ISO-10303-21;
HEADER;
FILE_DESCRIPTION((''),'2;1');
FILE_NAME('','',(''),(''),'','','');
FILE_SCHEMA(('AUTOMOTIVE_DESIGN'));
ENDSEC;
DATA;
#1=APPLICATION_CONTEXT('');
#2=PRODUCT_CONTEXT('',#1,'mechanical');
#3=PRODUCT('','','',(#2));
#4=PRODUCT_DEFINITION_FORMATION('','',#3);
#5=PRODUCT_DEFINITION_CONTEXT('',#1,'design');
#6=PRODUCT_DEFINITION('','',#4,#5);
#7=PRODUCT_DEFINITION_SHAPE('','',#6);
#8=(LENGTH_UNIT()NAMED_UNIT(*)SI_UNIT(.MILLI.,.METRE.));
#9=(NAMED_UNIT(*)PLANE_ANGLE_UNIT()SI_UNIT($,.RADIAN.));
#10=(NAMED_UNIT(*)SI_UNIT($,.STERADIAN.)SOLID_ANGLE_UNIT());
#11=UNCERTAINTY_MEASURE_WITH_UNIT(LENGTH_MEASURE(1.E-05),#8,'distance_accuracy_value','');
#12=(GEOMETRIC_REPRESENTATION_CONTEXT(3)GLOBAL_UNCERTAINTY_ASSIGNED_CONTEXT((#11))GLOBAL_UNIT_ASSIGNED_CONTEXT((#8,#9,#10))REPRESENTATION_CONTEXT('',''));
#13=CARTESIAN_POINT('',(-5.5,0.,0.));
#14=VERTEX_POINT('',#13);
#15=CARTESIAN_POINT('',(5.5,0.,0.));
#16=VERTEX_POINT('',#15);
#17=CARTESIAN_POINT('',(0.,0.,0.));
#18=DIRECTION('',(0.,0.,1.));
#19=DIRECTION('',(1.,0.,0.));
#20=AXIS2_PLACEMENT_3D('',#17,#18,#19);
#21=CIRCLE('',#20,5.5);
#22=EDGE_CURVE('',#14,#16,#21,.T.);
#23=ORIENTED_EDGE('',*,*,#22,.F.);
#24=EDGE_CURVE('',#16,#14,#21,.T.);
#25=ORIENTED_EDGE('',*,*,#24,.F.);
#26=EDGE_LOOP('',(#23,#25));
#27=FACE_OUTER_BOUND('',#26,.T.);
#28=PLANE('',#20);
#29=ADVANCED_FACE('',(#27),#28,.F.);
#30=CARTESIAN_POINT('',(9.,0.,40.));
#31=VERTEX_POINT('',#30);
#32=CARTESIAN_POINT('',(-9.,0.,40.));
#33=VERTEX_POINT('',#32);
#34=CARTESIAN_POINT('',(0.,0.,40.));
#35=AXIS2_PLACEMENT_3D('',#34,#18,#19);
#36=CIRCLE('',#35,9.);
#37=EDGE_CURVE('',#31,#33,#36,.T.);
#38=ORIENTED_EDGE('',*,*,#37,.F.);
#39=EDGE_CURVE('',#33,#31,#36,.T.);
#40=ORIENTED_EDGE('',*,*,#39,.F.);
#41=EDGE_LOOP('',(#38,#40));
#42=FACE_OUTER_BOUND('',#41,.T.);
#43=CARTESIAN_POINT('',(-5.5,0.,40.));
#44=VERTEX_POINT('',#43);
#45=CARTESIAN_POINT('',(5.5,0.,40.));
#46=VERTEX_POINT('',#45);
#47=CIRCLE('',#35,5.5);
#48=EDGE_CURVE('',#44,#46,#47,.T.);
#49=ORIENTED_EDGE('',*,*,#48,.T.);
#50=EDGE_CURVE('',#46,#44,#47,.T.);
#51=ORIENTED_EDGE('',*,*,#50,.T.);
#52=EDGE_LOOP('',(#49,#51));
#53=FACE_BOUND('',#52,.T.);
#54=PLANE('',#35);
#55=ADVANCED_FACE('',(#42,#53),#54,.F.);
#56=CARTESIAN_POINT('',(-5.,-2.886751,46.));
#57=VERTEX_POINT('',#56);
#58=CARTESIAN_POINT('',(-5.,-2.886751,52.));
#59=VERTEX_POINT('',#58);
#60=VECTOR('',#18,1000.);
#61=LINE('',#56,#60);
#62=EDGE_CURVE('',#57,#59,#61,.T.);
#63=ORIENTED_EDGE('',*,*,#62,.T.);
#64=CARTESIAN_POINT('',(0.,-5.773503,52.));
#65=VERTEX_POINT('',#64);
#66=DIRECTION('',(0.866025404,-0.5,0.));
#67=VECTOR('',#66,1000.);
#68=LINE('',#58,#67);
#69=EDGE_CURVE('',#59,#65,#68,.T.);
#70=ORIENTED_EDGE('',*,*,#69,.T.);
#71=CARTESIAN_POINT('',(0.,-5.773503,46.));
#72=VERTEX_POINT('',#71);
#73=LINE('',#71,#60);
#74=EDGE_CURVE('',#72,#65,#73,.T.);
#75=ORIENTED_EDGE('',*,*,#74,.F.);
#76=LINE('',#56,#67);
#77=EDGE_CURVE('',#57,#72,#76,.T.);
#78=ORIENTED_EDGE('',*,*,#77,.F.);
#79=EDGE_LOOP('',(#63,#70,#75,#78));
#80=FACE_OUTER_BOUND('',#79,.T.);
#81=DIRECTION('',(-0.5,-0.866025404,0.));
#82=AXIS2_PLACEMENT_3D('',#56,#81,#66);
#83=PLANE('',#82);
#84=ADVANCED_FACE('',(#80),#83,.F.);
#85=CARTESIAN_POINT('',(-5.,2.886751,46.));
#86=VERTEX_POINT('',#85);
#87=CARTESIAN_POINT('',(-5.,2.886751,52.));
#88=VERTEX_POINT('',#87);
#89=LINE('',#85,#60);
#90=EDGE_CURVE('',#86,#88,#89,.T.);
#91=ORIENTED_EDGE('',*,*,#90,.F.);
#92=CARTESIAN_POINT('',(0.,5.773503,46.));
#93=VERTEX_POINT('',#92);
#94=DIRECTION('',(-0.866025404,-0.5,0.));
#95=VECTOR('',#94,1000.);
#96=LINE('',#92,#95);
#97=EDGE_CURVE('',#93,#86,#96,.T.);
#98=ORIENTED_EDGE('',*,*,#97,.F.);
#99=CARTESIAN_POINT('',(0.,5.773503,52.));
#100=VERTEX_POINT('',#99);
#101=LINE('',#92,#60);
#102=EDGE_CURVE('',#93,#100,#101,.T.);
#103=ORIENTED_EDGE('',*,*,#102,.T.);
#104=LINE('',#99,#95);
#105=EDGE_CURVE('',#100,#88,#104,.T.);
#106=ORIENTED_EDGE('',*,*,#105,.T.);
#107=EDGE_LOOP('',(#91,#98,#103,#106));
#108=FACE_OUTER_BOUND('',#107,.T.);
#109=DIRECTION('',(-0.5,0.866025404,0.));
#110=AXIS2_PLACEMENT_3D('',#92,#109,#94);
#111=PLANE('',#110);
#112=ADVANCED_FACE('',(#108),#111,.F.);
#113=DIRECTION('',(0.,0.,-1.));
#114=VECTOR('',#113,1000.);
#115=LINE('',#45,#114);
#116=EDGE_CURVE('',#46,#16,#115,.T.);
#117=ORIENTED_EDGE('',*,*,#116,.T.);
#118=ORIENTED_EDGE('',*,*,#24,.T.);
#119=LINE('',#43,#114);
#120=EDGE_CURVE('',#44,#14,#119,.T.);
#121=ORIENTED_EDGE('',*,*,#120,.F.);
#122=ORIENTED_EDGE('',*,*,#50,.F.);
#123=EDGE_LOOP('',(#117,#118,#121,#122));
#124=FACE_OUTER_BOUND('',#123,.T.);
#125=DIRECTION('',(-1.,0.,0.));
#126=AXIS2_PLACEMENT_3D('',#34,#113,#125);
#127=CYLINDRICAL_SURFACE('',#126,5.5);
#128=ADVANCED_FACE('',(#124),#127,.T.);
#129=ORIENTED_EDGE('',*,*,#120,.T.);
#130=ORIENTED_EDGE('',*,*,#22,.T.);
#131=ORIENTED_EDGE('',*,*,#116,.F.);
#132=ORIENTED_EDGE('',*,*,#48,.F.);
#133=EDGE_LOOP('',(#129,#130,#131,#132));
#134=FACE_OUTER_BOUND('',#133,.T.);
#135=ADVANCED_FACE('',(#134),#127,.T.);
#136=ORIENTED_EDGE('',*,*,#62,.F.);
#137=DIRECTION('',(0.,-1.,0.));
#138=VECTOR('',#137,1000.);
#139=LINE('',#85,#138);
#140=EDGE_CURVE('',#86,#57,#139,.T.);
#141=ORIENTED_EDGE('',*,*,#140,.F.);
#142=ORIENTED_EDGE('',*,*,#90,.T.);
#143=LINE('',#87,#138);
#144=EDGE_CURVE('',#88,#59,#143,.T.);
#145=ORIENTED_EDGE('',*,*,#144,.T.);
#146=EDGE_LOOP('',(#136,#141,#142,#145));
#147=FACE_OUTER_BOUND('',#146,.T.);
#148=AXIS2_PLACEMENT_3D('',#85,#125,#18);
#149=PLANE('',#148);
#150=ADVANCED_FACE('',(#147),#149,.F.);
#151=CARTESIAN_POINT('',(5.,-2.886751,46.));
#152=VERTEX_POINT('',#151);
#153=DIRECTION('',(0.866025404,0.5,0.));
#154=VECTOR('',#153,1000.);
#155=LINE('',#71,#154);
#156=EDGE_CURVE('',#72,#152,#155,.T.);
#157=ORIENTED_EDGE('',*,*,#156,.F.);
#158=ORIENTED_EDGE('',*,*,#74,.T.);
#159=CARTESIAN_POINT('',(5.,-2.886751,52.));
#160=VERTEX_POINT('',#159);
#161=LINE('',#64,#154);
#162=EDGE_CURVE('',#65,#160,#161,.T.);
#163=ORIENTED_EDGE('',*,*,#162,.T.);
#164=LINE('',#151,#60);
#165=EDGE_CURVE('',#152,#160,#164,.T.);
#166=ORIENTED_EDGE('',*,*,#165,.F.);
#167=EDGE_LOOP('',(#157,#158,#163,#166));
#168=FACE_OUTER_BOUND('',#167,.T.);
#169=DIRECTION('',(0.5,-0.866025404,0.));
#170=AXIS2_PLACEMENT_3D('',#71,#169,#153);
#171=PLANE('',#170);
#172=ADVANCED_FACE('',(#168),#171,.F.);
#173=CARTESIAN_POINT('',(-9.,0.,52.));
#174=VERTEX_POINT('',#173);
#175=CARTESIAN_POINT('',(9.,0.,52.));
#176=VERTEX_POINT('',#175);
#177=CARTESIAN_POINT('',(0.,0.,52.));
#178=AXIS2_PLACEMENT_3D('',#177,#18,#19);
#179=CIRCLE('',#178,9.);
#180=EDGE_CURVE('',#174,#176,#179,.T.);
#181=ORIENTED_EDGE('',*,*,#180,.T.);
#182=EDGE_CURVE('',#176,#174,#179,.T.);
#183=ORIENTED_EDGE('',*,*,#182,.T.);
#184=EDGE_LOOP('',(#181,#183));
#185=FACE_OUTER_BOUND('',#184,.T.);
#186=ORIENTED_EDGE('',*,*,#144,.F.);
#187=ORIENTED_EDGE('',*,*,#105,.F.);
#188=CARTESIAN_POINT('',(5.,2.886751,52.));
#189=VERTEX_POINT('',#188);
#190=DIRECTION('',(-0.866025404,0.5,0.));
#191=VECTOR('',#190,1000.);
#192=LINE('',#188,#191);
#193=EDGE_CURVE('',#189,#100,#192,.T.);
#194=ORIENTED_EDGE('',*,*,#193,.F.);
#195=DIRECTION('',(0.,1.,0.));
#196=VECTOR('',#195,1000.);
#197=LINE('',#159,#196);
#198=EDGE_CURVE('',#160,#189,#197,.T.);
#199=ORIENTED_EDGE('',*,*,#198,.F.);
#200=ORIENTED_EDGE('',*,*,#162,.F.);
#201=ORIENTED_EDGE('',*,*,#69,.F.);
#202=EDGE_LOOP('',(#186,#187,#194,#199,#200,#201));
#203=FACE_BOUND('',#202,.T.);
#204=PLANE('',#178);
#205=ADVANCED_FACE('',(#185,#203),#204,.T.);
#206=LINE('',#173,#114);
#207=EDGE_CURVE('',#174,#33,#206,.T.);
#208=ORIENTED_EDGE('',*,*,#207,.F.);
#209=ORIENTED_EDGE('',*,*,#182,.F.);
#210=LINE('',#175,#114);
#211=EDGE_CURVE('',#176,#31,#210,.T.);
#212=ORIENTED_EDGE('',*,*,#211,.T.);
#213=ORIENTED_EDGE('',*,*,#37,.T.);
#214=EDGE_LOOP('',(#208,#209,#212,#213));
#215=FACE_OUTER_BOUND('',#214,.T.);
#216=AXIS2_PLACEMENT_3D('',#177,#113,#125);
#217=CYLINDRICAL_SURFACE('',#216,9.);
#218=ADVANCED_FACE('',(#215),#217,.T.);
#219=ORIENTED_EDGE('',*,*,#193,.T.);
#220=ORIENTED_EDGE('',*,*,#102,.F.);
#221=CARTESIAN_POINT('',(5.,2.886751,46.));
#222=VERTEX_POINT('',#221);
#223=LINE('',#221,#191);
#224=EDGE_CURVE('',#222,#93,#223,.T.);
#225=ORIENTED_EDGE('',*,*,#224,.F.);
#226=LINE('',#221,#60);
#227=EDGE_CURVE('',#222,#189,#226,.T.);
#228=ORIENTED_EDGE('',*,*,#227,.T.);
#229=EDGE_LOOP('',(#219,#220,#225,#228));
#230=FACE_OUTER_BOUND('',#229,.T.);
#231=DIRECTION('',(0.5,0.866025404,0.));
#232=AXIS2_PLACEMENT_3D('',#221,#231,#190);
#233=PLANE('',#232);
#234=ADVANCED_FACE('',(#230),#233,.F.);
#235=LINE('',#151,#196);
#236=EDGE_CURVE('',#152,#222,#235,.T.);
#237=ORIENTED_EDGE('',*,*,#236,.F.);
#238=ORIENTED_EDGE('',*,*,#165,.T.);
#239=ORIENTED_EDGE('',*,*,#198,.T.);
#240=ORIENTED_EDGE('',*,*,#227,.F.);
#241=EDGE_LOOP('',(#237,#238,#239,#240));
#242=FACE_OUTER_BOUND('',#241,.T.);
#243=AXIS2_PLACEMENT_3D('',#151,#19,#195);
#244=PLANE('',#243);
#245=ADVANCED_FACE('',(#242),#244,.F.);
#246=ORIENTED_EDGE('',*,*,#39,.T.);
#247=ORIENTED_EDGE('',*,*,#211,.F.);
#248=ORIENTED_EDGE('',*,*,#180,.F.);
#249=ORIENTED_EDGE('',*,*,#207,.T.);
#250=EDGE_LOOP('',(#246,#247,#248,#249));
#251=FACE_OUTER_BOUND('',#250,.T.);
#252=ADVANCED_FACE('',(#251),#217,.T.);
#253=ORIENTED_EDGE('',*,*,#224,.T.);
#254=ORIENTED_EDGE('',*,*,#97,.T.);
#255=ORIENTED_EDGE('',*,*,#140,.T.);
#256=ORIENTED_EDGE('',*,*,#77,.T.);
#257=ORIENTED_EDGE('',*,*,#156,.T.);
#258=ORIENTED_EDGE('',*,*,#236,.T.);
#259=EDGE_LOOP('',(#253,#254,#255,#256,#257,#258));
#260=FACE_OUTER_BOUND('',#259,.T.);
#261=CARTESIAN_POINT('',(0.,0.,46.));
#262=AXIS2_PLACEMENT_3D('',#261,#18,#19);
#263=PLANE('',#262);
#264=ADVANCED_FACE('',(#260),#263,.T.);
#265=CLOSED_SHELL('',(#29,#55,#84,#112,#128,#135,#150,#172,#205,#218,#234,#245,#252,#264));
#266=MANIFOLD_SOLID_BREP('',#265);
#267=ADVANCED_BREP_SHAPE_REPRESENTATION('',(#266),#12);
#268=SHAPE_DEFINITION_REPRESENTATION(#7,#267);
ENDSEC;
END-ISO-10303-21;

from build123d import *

# Parameters (mm, degrees)
SKETCH1_R           = 5.5
BOSS_EXTRUDE1_DEPTH = 40
SKETCH2_R           = 9
BOSS_EXTRUDE2_DEPTH = 12
CUT_EXTRUDE1_DEPTH  = 6


with BuildPart() as part:
    # Sketch1 → Boss-Extrude1 (new body)
    with BuildSketch(Plane.XY):
        Circle(SKETCH1_R)
    extrude(amount=BOSS_EXTRUDE1_DEPTH)

    # Sketch2 → Boss-Extrude2 (add)
    with BuildSketch(Plane.XY.offset(40)):
        Circle(SKETCH2_R)
    extrude(amount=BOSS_EXTRUDE2_DEPTH)

    # Sketch3 → Cut-Extrude1 (cut)
    with BuildSketch(Plane.XY.offset(52)):
        Polygon((0, 5.773502692), (-5, 2.886751346), (-5, -2.886751346), (0, -5.773502692), (5, -2.886751346), (5, 2.886751346), align=None)
    extrude(amount=-CUT_EXTRUDE1_DEPTH, mode=Mode.SUBTRACT)


solid = part.part
